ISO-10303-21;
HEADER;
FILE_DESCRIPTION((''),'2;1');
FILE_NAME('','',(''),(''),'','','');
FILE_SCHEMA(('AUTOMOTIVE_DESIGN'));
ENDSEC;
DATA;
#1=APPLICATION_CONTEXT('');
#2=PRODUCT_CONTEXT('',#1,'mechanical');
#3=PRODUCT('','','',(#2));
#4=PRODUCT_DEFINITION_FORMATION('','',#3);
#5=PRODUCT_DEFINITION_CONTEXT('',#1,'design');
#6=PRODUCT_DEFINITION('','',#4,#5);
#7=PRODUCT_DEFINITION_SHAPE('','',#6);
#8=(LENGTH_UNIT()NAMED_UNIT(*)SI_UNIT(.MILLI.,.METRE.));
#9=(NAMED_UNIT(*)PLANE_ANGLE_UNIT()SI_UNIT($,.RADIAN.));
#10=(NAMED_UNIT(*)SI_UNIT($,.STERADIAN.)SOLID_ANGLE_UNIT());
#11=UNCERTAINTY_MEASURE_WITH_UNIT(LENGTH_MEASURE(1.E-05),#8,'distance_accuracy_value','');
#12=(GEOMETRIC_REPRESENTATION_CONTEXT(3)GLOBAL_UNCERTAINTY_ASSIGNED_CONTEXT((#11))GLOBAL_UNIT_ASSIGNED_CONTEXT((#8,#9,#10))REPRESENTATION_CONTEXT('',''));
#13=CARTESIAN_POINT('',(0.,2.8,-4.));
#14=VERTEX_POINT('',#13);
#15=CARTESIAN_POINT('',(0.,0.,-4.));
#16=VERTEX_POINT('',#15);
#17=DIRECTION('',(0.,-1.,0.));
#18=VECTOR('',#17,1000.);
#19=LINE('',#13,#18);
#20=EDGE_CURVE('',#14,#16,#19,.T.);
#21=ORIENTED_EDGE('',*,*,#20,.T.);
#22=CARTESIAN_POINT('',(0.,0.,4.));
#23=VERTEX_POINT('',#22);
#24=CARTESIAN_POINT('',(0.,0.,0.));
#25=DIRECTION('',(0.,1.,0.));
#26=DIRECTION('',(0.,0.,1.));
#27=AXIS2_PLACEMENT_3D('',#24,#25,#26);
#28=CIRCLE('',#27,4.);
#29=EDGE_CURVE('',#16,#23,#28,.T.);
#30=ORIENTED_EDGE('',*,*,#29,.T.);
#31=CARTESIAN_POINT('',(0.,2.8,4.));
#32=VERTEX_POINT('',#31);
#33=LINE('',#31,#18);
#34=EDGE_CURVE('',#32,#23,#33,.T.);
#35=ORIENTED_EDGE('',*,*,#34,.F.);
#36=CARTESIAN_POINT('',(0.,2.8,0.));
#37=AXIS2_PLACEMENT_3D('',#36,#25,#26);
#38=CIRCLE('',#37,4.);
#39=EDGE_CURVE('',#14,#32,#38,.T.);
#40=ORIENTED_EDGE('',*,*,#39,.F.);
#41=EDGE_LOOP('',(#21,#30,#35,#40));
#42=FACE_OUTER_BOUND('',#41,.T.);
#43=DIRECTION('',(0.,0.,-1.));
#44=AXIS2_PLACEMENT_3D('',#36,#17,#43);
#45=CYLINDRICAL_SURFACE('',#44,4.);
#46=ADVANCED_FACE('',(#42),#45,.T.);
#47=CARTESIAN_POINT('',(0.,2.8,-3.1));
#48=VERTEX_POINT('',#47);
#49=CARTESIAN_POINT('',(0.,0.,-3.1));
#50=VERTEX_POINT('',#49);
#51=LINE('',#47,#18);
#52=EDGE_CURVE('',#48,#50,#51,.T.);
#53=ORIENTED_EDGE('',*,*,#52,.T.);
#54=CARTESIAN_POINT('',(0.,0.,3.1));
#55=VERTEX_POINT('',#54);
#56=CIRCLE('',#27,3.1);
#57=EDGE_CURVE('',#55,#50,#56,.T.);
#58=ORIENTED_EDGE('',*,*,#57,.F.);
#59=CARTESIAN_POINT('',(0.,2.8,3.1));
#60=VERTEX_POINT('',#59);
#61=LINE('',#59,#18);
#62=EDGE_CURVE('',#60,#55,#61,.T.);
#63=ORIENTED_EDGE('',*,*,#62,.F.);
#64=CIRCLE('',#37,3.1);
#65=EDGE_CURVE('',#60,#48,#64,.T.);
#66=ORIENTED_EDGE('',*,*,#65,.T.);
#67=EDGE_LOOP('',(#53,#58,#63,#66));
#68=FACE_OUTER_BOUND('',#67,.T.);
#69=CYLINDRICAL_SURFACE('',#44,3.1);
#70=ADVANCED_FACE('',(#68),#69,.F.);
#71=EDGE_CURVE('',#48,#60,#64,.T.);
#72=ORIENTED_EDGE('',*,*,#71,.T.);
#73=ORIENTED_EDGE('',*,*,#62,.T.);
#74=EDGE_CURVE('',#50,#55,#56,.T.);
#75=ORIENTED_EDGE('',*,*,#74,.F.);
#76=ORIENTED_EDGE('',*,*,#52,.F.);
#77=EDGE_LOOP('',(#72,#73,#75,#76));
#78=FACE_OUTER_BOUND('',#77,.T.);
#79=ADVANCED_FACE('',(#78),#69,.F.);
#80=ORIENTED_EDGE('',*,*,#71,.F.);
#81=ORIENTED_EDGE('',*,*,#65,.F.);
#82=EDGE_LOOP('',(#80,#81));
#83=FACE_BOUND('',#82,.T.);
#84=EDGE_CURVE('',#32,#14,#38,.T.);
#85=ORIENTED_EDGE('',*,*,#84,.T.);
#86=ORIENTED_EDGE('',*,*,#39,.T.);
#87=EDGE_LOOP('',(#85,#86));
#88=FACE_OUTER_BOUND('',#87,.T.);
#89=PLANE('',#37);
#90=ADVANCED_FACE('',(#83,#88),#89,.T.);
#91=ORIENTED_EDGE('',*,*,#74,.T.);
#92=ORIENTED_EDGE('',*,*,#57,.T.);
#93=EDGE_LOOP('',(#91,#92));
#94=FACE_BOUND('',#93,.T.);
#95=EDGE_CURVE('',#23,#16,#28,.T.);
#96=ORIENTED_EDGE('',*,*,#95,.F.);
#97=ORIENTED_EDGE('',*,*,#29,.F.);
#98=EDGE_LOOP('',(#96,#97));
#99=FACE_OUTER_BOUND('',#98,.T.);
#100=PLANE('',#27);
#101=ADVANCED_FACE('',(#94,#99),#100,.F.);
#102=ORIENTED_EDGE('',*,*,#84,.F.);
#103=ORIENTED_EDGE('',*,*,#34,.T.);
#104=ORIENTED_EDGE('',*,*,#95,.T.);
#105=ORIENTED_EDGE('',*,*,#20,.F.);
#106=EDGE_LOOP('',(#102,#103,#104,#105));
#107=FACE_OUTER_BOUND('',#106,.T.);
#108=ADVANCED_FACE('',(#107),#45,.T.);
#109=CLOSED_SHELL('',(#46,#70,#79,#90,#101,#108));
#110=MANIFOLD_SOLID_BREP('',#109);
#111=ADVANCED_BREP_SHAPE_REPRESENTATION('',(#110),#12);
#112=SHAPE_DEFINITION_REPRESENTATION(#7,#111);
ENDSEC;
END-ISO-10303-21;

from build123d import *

# Parameters (mm, degrees)
SKETCH1_R           = 4
SKETCH1_R_2         = 3.1
BOSS_EXTRUDE1_DEPTH = 2.8


with BuildPart() as part:
    # Sketch1 → Boss-Extrude1 (new body)
    with BuildSketch(Plane(origin=(0, 0, 0), x_dir=(1, 0, 0), z_dir=(0, 1, 0))):
        with Locations(Location((0, 0, 0), (0, 0, 270))):
            Circle(SKETCH1_R)
        with Locations(Location((0, 0, 0), (0, 0, 270))):
            Circle(SKETCH1_R_2, mode=Mode.SUBTRACT)
    extrude(amount=BOSS_EXTRUDE1_DEPTH)


solid = part.part
